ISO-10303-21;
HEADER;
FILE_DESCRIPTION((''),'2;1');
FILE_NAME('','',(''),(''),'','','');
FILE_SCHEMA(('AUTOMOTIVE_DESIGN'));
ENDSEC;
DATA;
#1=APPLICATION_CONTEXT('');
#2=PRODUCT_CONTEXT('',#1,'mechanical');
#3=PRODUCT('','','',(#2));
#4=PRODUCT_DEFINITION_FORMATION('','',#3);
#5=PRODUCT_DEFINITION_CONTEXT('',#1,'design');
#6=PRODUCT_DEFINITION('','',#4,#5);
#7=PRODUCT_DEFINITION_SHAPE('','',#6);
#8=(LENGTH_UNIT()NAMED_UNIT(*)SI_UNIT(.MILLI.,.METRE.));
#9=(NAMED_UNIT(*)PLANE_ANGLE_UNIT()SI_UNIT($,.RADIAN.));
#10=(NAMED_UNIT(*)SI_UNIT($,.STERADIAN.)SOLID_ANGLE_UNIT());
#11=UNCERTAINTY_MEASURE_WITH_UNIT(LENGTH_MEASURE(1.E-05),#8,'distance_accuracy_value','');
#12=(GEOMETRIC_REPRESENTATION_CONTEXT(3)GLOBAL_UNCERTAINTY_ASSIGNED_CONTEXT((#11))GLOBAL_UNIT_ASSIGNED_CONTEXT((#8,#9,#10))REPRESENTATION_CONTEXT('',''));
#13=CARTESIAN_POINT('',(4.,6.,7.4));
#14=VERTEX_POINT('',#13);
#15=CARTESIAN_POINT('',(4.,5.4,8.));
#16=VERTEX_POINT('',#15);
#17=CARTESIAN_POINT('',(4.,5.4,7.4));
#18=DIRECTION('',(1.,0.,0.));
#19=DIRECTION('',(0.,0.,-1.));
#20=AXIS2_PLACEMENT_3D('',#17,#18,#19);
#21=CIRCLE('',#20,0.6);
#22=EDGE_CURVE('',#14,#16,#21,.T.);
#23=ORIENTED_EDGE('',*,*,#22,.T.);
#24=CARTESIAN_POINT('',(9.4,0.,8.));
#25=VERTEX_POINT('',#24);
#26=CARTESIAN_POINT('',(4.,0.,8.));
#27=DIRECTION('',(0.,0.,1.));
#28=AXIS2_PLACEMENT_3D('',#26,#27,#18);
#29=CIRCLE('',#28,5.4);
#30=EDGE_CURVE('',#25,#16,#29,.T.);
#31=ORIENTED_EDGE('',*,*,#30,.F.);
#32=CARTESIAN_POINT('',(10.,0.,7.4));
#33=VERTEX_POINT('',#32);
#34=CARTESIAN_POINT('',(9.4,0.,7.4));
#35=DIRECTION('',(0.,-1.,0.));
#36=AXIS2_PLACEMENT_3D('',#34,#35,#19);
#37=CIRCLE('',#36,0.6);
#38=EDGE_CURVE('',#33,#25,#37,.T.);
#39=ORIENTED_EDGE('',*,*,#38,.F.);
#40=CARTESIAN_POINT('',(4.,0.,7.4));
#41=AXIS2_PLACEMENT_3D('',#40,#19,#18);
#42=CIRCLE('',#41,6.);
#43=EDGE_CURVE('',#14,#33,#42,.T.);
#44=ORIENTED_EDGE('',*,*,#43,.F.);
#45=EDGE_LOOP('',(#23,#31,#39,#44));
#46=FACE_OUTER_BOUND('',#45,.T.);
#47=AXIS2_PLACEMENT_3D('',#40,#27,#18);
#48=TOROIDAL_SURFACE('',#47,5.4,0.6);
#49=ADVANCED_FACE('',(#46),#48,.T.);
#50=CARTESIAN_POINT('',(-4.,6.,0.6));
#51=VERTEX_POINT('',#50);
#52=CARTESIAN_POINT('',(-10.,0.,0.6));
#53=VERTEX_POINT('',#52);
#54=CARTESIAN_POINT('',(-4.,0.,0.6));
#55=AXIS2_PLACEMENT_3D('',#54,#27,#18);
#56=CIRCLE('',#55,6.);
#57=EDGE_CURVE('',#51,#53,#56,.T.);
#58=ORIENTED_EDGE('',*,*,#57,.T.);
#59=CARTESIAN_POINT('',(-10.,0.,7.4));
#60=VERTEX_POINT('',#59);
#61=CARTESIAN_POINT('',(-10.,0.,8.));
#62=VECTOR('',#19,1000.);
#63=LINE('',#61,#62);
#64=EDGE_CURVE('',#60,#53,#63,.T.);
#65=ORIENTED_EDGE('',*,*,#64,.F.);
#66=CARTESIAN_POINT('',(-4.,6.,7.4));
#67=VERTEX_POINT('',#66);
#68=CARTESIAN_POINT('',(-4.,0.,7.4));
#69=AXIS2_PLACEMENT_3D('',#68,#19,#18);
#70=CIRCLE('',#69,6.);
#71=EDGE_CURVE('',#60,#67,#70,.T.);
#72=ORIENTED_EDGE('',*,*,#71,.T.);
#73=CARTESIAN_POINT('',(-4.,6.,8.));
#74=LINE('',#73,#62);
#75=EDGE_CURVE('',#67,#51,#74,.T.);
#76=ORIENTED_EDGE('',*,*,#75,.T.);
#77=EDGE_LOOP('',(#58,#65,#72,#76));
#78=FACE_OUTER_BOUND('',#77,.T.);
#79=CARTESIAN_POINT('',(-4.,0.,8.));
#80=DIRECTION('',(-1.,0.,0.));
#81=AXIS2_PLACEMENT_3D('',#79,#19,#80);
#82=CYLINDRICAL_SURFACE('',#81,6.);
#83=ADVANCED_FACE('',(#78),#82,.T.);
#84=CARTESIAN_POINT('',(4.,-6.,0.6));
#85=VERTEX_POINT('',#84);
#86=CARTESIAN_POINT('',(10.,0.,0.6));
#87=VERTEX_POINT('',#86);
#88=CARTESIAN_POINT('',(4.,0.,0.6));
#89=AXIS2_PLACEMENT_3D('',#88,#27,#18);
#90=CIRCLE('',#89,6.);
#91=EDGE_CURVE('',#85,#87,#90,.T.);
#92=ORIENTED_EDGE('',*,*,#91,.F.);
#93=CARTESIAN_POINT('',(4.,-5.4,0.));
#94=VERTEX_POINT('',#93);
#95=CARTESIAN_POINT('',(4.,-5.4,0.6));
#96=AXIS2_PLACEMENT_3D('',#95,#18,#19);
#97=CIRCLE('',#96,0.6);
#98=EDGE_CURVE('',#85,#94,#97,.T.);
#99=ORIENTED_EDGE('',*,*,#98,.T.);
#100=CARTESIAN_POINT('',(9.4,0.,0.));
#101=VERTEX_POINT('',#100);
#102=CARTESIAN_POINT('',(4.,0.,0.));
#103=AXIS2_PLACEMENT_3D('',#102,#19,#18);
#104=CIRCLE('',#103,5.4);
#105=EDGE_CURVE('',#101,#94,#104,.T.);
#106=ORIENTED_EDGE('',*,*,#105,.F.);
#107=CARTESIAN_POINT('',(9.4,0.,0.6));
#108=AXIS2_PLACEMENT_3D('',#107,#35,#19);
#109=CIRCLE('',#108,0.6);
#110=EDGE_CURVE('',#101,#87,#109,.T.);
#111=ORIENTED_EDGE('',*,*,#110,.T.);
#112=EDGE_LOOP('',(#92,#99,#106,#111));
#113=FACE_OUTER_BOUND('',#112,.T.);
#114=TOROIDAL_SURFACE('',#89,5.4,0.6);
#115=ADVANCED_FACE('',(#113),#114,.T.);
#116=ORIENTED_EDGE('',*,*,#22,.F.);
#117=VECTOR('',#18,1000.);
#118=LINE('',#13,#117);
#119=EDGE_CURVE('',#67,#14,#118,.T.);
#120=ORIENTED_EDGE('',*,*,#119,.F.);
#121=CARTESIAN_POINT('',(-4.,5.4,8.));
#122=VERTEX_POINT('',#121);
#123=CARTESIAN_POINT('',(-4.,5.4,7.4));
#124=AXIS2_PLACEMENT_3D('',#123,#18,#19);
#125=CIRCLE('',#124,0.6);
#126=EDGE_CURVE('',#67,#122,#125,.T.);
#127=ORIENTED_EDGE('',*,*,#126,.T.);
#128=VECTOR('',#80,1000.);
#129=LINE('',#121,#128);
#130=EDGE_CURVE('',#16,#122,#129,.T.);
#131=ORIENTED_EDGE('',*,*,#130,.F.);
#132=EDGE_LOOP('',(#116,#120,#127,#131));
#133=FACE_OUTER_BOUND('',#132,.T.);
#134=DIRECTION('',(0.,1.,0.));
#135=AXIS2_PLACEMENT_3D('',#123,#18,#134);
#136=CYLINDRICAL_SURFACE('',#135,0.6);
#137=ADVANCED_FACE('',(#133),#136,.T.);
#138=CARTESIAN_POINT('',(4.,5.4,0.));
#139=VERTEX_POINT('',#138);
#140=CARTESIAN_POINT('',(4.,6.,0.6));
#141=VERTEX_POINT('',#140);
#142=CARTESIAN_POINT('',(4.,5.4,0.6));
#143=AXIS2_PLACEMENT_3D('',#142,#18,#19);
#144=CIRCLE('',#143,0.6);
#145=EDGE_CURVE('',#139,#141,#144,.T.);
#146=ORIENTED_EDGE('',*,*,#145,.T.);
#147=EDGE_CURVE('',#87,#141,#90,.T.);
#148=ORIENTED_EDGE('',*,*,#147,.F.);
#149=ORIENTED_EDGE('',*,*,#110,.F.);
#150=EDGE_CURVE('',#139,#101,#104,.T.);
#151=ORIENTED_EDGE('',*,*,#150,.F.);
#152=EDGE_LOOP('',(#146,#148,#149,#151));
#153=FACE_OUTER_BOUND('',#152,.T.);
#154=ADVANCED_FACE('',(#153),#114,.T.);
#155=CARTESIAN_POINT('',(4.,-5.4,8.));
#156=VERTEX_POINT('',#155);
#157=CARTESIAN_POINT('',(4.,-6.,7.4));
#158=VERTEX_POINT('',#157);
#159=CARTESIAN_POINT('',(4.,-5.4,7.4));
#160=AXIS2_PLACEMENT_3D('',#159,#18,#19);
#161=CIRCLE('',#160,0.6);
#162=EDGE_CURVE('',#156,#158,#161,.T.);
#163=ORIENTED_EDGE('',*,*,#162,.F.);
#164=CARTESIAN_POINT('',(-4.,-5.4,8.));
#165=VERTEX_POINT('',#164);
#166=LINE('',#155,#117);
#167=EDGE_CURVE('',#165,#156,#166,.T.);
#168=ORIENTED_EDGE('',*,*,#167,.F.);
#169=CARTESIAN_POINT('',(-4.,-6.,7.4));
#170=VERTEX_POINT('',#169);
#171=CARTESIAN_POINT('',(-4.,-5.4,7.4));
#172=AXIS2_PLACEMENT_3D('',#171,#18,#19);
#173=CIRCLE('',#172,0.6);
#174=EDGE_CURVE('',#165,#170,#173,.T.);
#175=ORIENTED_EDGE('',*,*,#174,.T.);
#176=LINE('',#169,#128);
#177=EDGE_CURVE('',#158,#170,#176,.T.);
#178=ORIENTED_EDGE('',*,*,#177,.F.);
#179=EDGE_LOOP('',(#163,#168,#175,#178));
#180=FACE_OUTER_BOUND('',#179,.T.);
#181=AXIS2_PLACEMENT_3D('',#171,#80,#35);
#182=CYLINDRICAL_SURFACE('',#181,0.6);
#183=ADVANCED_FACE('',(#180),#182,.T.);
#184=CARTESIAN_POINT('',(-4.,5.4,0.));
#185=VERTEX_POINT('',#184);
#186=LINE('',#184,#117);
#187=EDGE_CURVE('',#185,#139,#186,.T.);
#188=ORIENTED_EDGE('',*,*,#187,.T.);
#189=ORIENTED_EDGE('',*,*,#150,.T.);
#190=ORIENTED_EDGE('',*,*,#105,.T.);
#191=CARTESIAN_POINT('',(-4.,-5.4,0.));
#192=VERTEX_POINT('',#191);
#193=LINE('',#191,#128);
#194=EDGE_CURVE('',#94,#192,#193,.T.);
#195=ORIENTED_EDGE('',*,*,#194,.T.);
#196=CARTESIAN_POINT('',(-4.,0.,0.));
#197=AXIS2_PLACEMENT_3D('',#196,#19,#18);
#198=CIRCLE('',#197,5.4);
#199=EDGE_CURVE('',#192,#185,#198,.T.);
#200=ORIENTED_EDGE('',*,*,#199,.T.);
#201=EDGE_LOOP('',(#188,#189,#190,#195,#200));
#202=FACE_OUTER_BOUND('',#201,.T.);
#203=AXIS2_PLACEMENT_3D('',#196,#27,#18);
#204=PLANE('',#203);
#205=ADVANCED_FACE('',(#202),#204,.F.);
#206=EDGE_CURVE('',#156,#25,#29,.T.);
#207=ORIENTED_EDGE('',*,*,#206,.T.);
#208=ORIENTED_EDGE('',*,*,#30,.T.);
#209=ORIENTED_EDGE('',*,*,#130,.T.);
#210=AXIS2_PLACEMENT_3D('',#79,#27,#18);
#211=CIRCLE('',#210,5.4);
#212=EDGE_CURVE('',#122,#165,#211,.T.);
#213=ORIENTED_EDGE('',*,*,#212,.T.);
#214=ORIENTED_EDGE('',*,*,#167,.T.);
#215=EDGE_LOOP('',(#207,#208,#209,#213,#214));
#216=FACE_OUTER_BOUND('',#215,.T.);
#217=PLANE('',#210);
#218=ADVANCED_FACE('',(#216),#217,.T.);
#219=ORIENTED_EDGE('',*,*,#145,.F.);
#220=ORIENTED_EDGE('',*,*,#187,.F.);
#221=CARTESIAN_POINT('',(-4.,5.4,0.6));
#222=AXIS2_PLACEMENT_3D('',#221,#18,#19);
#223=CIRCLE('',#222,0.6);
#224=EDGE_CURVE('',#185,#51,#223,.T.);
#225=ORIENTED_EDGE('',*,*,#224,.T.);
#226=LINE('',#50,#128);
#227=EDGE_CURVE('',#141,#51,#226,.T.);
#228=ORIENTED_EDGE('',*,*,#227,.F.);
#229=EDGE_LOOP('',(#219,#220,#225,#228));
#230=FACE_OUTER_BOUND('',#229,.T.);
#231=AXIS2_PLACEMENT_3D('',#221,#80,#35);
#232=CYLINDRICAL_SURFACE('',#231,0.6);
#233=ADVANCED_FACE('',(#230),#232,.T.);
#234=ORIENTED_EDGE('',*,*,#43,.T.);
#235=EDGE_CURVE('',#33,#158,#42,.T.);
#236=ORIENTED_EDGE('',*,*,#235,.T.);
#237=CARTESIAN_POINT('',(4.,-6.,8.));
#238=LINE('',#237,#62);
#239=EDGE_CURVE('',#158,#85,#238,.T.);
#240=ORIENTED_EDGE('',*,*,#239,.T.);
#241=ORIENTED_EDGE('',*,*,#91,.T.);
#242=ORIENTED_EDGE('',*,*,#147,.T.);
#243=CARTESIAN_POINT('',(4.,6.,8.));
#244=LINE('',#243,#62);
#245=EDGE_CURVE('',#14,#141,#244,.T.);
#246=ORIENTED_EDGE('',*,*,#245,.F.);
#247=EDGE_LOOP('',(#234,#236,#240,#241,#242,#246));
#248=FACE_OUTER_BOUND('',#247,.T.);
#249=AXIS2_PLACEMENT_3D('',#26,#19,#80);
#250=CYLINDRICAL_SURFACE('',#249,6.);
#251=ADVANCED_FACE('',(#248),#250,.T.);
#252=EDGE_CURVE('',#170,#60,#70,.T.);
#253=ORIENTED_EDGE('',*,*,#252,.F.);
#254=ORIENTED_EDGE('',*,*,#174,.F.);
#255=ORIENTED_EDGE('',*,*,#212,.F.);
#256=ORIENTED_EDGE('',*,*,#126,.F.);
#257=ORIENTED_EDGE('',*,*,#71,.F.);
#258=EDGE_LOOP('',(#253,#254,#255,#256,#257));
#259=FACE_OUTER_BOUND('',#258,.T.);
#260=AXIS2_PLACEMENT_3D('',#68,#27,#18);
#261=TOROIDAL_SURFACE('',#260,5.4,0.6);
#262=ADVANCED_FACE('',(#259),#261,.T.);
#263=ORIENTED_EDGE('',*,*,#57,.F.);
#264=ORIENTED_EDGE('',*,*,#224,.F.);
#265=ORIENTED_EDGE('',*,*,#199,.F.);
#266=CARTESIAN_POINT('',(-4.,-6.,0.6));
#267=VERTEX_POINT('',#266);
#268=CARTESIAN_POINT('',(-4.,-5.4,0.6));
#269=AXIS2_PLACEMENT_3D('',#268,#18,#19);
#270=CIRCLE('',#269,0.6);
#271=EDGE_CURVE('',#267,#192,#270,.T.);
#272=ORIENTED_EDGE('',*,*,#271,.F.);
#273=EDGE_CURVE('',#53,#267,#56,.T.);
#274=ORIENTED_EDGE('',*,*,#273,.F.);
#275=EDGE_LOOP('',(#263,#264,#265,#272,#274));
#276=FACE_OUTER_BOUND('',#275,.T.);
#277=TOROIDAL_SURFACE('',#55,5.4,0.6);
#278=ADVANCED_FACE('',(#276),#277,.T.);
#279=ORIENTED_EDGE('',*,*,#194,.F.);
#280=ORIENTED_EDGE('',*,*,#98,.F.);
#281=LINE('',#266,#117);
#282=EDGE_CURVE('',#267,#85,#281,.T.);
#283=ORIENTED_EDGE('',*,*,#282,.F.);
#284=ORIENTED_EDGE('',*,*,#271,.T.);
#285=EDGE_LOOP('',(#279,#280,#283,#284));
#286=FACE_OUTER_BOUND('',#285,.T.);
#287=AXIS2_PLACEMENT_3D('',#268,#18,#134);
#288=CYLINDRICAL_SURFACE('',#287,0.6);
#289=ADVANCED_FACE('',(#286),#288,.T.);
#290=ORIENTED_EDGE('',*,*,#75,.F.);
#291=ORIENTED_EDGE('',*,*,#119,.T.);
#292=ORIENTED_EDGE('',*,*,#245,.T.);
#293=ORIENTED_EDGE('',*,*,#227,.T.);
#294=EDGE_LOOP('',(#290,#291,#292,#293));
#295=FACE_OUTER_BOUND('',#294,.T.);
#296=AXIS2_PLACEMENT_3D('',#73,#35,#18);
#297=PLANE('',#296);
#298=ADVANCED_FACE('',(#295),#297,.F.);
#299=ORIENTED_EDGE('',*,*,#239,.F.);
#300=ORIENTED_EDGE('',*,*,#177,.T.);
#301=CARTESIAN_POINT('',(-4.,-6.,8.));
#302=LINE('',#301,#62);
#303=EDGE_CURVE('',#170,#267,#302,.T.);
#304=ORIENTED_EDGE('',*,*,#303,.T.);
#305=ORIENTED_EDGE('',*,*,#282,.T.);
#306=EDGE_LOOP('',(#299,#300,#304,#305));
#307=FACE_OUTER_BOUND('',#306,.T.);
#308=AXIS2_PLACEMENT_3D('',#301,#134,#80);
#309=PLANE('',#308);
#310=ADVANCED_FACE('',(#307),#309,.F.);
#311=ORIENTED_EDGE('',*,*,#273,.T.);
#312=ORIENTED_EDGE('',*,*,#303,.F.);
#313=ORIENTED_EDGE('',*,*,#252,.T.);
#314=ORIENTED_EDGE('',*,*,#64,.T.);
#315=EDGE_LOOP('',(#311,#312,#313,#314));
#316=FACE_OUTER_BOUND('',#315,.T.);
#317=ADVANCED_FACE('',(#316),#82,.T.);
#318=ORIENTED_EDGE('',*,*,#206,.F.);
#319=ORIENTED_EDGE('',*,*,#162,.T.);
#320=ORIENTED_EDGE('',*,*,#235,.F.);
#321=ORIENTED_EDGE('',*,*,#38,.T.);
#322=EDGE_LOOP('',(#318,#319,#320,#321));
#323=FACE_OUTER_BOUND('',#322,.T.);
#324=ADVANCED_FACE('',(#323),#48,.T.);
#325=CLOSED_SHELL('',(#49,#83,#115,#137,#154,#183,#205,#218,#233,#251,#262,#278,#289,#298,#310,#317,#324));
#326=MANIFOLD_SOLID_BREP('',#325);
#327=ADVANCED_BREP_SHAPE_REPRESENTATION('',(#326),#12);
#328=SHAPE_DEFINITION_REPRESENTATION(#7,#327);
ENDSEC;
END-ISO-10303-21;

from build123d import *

# Parameters (mm, degrees)
EXTRUDE_523_DEPTH = 8
FILLET_1_R        = 0.6


with BuildPart() as part:
    # 草图1 → Extrude 523 (new body)
    with BuildSketch(Plane.XY):
        with BuildLine():
            Line((-4, 6), (4, 6))
            ThreePointArc((4, 6), (10, 0), (4, -6))
            Line((4, -6), (-4, -6))
            ThreePointArc((-4, -6), (-10, 0), (-4, 6))
        make_face()
    extrude(amount=EXTRUDE_523_DEPTH)

    # 圆角1
    fillet_1_edges = [part.edges().sort_by_distance(p)[0] for p in [
        (10, 0, 8),
        (0, 6, 8),
        (-10, 0, 8),
        (0, 6, 0),
        (10, 0, 0),
        (0, -6, 0),
        (-10, 0, 0),
        (0, -6, 8),
    ]]
    fillet(fillet_1_edges, radius=FILLET_1_R)


solid = part.part
